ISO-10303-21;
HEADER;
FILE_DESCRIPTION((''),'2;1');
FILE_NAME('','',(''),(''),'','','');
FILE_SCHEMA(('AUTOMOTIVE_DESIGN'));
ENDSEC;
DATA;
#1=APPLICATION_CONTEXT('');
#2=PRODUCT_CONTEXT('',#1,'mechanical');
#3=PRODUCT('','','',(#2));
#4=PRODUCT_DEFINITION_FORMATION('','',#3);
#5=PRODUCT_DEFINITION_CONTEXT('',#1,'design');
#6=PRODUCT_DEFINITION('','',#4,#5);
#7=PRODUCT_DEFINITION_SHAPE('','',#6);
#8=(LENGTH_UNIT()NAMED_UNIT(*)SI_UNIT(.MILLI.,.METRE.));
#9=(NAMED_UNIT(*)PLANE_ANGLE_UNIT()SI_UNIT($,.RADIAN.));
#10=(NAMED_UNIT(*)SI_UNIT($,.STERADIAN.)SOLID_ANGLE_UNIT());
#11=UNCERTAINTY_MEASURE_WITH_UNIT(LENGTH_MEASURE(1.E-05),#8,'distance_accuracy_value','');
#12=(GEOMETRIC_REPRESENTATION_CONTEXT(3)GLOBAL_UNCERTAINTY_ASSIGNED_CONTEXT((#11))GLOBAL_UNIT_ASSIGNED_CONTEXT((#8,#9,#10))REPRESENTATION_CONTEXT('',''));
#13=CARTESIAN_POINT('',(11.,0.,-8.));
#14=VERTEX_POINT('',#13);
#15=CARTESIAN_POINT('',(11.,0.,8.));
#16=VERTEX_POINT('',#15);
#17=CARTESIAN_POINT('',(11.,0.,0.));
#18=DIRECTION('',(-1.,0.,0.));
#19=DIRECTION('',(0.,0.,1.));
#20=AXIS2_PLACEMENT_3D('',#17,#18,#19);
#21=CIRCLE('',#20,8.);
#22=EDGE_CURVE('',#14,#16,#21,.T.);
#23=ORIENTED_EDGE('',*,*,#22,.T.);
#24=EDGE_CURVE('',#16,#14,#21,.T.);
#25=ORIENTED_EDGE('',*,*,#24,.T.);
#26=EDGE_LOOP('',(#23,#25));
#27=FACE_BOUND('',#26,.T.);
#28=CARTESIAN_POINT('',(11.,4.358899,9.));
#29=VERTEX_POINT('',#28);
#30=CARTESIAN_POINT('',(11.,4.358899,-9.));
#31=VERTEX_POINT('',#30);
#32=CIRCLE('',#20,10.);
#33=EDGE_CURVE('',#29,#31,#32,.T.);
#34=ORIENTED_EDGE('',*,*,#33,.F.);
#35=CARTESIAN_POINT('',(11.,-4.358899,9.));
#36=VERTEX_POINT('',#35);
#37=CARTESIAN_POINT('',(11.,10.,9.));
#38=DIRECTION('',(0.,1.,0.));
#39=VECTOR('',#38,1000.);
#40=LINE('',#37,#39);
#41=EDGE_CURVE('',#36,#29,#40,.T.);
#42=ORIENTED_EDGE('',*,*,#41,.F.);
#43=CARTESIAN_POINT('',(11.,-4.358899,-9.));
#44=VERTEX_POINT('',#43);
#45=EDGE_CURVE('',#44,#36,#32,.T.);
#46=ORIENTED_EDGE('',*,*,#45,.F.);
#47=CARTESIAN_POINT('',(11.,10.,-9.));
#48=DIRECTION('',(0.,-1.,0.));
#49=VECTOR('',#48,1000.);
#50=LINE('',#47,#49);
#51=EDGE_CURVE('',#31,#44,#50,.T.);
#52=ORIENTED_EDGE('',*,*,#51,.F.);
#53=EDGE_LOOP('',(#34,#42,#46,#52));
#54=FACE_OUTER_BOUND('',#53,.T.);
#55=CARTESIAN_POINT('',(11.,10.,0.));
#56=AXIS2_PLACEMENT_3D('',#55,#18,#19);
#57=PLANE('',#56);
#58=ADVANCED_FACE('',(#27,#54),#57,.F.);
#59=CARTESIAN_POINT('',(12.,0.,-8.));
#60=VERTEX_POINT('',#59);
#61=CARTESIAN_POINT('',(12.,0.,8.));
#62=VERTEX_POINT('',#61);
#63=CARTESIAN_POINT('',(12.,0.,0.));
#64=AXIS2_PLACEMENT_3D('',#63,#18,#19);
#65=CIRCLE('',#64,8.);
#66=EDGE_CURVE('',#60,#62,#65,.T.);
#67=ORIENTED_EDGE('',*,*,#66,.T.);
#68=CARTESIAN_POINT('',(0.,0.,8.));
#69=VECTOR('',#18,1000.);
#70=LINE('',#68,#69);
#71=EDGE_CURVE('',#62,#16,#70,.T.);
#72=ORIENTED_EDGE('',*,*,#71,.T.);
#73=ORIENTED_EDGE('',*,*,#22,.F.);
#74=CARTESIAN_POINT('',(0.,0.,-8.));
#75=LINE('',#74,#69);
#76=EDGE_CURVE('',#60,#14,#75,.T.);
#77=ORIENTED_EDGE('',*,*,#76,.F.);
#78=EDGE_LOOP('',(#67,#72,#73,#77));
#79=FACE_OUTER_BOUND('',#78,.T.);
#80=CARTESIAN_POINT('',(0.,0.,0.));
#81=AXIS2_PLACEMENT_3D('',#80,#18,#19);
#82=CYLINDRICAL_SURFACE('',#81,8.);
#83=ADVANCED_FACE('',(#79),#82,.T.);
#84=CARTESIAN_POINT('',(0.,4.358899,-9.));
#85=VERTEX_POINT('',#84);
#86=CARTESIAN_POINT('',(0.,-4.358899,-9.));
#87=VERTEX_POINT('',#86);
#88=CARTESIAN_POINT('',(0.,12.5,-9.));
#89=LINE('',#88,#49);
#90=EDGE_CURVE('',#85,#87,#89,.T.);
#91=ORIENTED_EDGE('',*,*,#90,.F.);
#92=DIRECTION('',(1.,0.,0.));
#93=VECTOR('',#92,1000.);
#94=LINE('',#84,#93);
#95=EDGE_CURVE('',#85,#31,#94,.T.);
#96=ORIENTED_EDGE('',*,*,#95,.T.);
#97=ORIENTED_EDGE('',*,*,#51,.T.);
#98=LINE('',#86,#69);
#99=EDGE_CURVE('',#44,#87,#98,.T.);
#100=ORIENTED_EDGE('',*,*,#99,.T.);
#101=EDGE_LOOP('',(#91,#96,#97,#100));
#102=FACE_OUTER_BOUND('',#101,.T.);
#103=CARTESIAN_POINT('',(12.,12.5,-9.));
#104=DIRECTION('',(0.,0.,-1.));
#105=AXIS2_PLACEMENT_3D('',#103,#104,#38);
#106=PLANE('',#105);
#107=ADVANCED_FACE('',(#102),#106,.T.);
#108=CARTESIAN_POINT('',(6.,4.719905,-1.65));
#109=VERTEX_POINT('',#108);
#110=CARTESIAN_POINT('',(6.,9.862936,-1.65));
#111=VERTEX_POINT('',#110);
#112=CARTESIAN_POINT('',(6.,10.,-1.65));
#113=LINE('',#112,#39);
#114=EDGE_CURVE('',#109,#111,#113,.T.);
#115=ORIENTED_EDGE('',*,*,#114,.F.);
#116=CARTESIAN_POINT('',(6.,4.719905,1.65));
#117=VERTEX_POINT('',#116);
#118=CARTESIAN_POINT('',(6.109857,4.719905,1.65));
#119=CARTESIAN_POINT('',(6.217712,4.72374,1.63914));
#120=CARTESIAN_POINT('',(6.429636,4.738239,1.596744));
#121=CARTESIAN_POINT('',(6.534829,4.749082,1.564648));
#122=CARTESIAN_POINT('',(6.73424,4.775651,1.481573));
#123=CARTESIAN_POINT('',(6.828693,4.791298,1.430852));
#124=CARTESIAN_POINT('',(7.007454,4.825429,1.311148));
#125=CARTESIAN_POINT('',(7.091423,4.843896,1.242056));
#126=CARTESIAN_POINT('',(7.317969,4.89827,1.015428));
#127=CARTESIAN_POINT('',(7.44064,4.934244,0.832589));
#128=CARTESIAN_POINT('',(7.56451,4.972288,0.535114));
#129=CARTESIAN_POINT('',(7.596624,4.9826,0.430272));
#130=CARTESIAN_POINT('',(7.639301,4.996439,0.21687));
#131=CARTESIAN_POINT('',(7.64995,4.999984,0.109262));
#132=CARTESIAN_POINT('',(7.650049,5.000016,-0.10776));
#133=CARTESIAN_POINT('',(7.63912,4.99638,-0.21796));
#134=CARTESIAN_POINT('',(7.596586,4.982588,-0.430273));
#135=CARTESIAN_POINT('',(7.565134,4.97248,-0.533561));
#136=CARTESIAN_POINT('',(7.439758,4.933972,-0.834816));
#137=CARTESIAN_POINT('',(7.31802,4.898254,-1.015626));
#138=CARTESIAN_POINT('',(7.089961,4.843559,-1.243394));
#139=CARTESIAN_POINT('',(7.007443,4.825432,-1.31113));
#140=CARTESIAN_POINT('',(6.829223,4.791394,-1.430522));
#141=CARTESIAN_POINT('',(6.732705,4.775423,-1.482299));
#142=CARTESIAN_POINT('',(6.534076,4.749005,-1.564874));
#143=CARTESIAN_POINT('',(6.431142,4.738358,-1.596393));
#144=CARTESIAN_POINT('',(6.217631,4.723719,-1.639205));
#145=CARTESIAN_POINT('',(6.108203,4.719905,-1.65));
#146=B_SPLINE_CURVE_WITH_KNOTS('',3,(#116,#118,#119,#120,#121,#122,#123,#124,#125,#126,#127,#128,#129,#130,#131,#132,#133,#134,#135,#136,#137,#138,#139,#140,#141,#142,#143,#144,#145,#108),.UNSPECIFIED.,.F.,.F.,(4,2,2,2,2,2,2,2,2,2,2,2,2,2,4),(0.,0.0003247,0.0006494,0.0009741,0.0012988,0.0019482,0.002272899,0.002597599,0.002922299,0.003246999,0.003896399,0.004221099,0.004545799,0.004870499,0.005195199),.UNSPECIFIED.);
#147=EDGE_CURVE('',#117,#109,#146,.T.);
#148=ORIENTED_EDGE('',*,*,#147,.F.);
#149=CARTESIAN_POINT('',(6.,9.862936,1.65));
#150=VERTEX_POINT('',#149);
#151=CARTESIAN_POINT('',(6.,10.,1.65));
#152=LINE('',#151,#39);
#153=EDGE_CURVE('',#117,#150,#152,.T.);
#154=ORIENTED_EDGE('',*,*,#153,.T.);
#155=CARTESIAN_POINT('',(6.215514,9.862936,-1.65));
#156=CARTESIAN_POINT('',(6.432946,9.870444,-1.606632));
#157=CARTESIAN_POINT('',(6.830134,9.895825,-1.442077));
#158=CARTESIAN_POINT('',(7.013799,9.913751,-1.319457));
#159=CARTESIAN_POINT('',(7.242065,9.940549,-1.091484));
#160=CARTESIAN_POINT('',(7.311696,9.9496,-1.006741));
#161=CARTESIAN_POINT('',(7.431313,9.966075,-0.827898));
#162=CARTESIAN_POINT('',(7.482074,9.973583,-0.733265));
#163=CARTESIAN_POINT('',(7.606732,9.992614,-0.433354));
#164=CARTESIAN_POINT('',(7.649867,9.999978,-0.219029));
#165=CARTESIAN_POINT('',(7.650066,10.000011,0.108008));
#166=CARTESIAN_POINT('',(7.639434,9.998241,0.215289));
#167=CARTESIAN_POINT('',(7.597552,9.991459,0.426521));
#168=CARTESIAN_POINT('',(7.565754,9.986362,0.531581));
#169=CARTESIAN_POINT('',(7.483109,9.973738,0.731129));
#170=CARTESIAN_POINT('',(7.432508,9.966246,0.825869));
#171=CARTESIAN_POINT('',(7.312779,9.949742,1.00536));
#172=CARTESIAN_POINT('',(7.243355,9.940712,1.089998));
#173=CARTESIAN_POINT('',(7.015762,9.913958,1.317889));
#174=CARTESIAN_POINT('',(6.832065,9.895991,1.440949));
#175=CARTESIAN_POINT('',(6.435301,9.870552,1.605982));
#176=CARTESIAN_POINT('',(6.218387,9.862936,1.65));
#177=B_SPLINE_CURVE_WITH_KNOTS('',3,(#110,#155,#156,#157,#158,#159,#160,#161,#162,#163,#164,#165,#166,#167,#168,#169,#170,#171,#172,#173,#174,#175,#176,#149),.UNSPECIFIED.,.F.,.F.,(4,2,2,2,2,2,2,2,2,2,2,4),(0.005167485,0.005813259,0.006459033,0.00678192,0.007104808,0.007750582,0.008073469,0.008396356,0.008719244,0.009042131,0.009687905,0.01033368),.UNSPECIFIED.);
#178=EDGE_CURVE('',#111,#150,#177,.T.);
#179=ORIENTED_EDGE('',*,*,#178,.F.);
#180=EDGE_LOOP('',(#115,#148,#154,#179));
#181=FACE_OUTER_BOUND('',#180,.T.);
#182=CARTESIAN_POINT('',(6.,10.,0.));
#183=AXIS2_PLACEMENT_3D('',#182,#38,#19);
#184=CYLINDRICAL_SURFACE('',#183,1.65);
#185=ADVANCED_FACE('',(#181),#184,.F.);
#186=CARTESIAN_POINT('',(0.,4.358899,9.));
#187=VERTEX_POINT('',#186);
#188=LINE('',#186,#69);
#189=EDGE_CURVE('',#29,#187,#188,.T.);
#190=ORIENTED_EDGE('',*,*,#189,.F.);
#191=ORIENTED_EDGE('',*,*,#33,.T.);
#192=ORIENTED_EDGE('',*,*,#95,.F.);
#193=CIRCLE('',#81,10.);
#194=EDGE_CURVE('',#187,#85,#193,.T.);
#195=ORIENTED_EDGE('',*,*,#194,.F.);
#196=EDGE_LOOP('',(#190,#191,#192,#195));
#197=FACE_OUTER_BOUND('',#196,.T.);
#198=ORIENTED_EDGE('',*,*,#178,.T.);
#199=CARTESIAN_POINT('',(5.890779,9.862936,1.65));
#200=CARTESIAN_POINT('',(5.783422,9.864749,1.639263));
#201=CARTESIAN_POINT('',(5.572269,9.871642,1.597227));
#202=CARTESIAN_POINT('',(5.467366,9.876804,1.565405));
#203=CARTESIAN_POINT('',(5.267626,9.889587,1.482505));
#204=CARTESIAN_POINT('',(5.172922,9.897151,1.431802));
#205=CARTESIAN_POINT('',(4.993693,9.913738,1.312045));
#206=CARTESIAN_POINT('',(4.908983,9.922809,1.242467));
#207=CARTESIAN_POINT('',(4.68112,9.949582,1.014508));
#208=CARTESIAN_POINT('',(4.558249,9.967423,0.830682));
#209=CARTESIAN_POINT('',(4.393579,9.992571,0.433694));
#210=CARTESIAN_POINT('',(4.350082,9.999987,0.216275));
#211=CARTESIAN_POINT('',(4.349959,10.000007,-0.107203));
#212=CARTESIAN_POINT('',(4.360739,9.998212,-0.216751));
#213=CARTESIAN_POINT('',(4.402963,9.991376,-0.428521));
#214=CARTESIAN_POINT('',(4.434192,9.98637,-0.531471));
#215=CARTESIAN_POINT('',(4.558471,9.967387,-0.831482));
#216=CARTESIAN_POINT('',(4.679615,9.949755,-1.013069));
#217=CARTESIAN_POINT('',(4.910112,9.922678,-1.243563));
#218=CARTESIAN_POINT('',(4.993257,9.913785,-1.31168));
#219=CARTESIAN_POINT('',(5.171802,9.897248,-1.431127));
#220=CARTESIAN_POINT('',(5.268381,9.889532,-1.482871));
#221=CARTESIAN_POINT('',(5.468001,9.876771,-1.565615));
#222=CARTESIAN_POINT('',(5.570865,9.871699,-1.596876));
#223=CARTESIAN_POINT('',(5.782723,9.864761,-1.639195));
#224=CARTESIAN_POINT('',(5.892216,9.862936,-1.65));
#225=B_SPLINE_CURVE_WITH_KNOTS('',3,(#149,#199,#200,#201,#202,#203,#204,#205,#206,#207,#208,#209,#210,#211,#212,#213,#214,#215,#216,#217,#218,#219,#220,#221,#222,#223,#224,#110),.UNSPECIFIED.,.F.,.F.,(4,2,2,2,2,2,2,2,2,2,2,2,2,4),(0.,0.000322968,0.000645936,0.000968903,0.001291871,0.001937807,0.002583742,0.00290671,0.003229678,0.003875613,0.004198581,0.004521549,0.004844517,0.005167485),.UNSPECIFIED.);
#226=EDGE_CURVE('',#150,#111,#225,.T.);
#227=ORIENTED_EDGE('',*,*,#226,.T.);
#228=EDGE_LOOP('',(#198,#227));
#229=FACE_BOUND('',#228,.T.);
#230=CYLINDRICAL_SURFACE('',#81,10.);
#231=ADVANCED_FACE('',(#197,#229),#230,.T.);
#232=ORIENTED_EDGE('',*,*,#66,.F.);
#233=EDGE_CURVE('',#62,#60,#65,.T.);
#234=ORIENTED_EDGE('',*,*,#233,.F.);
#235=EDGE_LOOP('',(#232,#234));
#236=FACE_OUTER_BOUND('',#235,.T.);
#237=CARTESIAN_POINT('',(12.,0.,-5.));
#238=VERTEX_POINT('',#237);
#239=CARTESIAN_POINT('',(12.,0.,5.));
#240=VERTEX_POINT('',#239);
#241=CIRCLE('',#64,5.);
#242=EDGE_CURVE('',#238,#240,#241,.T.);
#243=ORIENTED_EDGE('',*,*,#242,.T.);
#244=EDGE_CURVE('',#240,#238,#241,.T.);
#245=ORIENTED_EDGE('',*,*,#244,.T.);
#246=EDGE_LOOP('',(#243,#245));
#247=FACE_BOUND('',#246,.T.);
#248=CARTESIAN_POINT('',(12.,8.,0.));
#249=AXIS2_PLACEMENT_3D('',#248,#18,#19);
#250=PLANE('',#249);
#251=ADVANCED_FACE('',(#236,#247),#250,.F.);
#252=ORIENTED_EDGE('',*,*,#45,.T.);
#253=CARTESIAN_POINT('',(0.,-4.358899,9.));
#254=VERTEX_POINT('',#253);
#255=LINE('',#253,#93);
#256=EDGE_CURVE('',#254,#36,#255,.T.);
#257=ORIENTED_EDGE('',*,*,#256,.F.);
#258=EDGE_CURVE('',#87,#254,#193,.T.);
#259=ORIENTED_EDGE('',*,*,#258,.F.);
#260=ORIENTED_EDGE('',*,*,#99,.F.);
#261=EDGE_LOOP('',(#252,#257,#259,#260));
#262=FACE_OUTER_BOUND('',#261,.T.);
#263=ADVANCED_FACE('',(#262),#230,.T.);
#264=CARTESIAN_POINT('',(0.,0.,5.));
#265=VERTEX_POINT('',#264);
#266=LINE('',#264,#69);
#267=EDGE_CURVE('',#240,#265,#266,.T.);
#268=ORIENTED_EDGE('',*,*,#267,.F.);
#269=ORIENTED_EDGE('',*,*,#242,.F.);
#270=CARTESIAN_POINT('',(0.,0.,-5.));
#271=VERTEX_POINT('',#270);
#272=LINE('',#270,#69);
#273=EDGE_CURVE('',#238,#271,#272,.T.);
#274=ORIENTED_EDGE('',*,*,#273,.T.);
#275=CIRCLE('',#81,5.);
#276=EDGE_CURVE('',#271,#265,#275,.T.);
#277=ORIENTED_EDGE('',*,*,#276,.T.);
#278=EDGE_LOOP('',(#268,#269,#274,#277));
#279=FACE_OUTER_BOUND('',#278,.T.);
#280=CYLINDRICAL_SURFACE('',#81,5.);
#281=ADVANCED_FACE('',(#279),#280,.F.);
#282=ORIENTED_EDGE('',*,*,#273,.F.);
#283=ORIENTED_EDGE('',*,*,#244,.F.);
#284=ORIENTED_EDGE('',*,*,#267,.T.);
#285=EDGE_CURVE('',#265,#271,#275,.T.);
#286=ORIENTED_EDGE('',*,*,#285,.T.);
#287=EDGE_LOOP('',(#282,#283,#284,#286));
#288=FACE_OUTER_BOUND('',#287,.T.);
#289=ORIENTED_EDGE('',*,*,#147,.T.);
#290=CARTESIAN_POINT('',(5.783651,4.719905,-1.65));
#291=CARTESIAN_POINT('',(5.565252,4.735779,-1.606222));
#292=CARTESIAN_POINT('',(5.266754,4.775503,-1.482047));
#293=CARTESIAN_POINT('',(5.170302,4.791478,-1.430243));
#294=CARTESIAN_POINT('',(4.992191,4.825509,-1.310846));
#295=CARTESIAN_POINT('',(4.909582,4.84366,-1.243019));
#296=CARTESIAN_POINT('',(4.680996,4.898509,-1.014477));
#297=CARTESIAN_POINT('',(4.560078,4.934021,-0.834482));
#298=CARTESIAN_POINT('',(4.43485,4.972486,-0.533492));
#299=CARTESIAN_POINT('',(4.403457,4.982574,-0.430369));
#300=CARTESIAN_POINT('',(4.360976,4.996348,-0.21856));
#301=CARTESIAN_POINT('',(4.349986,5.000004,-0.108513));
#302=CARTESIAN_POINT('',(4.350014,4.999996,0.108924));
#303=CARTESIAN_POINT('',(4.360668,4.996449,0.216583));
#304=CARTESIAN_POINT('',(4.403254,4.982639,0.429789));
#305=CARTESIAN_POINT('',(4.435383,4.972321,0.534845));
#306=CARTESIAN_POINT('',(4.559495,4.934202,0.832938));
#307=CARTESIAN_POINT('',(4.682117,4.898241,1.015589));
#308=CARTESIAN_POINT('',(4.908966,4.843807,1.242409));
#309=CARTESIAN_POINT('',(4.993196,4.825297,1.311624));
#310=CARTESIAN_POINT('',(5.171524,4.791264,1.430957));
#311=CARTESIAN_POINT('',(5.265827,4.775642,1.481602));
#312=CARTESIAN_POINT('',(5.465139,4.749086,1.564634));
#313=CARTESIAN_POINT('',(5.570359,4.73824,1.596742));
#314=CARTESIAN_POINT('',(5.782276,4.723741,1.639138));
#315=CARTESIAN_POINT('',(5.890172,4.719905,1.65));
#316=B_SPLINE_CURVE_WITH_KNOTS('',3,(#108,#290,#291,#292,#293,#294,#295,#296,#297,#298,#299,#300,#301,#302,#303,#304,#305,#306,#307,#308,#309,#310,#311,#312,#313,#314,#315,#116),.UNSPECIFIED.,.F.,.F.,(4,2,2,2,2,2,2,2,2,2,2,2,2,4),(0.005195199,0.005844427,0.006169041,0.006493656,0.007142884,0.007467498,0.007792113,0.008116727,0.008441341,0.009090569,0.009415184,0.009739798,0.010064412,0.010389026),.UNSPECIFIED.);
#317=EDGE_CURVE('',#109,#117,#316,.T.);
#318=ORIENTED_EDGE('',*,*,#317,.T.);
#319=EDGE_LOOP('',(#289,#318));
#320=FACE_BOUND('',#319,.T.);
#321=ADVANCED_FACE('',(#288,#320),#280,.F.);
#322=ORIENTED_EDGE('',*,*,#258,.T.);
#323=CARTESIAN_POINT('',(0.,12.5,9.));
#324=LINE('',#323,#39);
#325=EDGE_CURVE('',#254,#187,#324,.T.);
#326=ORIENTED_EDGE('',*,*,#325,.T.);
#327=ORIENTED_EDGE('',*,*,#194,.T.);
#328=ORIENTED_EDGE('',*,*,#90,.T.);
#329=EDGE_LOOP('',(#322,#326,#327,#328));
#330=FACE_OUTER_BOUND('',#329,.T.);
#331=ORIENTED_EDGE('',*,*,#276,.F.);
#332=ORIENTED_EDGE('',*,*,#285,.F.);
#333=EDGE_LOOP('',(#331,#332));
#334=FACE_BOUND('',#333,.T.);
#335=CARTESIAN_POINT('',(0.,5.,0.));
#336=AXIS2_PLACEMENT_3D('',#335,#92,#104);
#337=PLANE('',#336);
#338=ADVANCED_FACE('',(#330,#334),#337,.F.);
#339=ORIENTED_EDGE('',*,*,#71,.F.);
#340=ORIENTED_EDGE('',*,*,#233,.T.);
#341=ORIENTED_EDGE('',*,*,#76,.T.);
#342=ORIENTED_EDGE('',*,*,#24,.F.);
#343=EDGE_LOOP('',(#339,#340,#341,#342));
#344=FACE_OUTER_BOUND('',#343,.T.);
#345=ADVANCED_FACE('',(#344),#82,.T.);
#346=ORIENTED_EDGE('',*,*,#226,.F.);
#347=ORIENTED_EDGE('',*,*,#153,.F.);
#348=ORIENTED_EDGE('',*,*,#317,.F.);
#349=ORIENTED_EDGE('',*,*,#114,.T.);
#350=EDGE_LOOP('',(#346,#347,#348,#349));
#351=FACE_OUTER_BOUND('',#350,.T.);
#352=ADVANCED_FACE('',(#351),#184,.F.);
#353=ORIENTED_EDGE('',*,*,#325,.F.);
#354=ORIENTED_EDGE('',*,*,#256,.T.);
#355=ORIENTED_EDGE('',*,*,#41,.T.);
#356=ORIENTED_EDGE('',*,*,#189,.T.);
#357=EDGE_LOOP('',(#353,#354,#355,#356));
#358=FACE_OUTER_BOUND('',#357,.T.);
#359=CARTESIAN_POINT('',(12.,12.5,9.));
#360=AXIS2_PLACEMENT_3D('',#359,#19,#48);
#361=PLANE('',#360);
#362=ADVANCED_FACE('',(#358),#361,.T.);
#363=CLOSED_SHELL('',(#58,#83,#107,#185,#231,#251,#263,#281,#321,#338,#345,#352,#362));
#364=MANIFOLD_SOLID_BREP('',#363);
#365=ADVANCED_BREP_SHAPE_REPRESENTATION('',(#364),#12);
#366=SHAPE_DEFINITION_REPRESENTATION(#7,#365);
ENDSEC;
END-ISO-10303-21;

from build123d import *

# Parameters (mm, degrees)
SKETCH2_OUTSIDE_W      = 28.144
SKETCH2_OUTSIDE_H      = 28.144
SKETCH2_OUTSIDE_W_2    = 18
SKETCH2_OUTSIDE_H_2    = 25
CUT_EXTRUDE1_DEPTH     = 19.547236991
M4_TAPPED_HOLE1_REACH  = 27
M4_TAPPED_HOLE1_BORE_R = 1.65


with BuildPart() as part:
    # Sketch1 → Revolve1 (revolve)
    with BuildSketch(Plane.XY, mode=Mode.PRIVATE) as revolve1_sk:
        Polygon((0, 5), (0, 10), (11, 10), (11, 8), (12, 8), (12, 5), align=None)
    revolve(revolve1_sk.sketch.rotate(Axis((0, 0, 0), (1, 0, 0)), 90), axis=Axis((0, 0, 0), (1, 0, 0)))

    # Sketch2 outside → Cut-Extrude1 (cut, through all)
    with BuildSketch(Plane.ZY):
        Rectangle(SKETCH2_OUTSIDE_W, SKETCH2_OUTSIDE_H)
        Rectangle(SKETCH2_OUTSIDE_W_2, SKETCH2_OUTSIDE_H_2, mode=Mode.SUBTRACT)
    extrude(amount=-CUT_EXTRUDE1_DEPTH, mode=Mode.SUBTRACT)

    # M4 Tapped Hole1 bore → M4 Tapped Hole1 (cut, up to next)
    with BuildSketch(Plane(origin=(0, 10, 0), x_dir=(-1, 0, 0), z_dir=(0, 1, 0)), mode=Mode.PRIVATE) as m4_tapped_hole1_sk1:
        with Locations((-6, 0)):
            Circle(M4_TAPPED_HOLE1_BORE_R)
    m4_tapped_hole1_tool1 = extrude(m4_tapped_hole1_sk1.sketch, amount=-M4_TAPPED_HOLE1_REACH, mode=Mode.PRIVATE) & part.part
    add(m4_tapped_hole1_tool1.solids().sort_by_distance((6, 10, 0))[0], mode=Mode.SUBTRACT)


solid = part.part
